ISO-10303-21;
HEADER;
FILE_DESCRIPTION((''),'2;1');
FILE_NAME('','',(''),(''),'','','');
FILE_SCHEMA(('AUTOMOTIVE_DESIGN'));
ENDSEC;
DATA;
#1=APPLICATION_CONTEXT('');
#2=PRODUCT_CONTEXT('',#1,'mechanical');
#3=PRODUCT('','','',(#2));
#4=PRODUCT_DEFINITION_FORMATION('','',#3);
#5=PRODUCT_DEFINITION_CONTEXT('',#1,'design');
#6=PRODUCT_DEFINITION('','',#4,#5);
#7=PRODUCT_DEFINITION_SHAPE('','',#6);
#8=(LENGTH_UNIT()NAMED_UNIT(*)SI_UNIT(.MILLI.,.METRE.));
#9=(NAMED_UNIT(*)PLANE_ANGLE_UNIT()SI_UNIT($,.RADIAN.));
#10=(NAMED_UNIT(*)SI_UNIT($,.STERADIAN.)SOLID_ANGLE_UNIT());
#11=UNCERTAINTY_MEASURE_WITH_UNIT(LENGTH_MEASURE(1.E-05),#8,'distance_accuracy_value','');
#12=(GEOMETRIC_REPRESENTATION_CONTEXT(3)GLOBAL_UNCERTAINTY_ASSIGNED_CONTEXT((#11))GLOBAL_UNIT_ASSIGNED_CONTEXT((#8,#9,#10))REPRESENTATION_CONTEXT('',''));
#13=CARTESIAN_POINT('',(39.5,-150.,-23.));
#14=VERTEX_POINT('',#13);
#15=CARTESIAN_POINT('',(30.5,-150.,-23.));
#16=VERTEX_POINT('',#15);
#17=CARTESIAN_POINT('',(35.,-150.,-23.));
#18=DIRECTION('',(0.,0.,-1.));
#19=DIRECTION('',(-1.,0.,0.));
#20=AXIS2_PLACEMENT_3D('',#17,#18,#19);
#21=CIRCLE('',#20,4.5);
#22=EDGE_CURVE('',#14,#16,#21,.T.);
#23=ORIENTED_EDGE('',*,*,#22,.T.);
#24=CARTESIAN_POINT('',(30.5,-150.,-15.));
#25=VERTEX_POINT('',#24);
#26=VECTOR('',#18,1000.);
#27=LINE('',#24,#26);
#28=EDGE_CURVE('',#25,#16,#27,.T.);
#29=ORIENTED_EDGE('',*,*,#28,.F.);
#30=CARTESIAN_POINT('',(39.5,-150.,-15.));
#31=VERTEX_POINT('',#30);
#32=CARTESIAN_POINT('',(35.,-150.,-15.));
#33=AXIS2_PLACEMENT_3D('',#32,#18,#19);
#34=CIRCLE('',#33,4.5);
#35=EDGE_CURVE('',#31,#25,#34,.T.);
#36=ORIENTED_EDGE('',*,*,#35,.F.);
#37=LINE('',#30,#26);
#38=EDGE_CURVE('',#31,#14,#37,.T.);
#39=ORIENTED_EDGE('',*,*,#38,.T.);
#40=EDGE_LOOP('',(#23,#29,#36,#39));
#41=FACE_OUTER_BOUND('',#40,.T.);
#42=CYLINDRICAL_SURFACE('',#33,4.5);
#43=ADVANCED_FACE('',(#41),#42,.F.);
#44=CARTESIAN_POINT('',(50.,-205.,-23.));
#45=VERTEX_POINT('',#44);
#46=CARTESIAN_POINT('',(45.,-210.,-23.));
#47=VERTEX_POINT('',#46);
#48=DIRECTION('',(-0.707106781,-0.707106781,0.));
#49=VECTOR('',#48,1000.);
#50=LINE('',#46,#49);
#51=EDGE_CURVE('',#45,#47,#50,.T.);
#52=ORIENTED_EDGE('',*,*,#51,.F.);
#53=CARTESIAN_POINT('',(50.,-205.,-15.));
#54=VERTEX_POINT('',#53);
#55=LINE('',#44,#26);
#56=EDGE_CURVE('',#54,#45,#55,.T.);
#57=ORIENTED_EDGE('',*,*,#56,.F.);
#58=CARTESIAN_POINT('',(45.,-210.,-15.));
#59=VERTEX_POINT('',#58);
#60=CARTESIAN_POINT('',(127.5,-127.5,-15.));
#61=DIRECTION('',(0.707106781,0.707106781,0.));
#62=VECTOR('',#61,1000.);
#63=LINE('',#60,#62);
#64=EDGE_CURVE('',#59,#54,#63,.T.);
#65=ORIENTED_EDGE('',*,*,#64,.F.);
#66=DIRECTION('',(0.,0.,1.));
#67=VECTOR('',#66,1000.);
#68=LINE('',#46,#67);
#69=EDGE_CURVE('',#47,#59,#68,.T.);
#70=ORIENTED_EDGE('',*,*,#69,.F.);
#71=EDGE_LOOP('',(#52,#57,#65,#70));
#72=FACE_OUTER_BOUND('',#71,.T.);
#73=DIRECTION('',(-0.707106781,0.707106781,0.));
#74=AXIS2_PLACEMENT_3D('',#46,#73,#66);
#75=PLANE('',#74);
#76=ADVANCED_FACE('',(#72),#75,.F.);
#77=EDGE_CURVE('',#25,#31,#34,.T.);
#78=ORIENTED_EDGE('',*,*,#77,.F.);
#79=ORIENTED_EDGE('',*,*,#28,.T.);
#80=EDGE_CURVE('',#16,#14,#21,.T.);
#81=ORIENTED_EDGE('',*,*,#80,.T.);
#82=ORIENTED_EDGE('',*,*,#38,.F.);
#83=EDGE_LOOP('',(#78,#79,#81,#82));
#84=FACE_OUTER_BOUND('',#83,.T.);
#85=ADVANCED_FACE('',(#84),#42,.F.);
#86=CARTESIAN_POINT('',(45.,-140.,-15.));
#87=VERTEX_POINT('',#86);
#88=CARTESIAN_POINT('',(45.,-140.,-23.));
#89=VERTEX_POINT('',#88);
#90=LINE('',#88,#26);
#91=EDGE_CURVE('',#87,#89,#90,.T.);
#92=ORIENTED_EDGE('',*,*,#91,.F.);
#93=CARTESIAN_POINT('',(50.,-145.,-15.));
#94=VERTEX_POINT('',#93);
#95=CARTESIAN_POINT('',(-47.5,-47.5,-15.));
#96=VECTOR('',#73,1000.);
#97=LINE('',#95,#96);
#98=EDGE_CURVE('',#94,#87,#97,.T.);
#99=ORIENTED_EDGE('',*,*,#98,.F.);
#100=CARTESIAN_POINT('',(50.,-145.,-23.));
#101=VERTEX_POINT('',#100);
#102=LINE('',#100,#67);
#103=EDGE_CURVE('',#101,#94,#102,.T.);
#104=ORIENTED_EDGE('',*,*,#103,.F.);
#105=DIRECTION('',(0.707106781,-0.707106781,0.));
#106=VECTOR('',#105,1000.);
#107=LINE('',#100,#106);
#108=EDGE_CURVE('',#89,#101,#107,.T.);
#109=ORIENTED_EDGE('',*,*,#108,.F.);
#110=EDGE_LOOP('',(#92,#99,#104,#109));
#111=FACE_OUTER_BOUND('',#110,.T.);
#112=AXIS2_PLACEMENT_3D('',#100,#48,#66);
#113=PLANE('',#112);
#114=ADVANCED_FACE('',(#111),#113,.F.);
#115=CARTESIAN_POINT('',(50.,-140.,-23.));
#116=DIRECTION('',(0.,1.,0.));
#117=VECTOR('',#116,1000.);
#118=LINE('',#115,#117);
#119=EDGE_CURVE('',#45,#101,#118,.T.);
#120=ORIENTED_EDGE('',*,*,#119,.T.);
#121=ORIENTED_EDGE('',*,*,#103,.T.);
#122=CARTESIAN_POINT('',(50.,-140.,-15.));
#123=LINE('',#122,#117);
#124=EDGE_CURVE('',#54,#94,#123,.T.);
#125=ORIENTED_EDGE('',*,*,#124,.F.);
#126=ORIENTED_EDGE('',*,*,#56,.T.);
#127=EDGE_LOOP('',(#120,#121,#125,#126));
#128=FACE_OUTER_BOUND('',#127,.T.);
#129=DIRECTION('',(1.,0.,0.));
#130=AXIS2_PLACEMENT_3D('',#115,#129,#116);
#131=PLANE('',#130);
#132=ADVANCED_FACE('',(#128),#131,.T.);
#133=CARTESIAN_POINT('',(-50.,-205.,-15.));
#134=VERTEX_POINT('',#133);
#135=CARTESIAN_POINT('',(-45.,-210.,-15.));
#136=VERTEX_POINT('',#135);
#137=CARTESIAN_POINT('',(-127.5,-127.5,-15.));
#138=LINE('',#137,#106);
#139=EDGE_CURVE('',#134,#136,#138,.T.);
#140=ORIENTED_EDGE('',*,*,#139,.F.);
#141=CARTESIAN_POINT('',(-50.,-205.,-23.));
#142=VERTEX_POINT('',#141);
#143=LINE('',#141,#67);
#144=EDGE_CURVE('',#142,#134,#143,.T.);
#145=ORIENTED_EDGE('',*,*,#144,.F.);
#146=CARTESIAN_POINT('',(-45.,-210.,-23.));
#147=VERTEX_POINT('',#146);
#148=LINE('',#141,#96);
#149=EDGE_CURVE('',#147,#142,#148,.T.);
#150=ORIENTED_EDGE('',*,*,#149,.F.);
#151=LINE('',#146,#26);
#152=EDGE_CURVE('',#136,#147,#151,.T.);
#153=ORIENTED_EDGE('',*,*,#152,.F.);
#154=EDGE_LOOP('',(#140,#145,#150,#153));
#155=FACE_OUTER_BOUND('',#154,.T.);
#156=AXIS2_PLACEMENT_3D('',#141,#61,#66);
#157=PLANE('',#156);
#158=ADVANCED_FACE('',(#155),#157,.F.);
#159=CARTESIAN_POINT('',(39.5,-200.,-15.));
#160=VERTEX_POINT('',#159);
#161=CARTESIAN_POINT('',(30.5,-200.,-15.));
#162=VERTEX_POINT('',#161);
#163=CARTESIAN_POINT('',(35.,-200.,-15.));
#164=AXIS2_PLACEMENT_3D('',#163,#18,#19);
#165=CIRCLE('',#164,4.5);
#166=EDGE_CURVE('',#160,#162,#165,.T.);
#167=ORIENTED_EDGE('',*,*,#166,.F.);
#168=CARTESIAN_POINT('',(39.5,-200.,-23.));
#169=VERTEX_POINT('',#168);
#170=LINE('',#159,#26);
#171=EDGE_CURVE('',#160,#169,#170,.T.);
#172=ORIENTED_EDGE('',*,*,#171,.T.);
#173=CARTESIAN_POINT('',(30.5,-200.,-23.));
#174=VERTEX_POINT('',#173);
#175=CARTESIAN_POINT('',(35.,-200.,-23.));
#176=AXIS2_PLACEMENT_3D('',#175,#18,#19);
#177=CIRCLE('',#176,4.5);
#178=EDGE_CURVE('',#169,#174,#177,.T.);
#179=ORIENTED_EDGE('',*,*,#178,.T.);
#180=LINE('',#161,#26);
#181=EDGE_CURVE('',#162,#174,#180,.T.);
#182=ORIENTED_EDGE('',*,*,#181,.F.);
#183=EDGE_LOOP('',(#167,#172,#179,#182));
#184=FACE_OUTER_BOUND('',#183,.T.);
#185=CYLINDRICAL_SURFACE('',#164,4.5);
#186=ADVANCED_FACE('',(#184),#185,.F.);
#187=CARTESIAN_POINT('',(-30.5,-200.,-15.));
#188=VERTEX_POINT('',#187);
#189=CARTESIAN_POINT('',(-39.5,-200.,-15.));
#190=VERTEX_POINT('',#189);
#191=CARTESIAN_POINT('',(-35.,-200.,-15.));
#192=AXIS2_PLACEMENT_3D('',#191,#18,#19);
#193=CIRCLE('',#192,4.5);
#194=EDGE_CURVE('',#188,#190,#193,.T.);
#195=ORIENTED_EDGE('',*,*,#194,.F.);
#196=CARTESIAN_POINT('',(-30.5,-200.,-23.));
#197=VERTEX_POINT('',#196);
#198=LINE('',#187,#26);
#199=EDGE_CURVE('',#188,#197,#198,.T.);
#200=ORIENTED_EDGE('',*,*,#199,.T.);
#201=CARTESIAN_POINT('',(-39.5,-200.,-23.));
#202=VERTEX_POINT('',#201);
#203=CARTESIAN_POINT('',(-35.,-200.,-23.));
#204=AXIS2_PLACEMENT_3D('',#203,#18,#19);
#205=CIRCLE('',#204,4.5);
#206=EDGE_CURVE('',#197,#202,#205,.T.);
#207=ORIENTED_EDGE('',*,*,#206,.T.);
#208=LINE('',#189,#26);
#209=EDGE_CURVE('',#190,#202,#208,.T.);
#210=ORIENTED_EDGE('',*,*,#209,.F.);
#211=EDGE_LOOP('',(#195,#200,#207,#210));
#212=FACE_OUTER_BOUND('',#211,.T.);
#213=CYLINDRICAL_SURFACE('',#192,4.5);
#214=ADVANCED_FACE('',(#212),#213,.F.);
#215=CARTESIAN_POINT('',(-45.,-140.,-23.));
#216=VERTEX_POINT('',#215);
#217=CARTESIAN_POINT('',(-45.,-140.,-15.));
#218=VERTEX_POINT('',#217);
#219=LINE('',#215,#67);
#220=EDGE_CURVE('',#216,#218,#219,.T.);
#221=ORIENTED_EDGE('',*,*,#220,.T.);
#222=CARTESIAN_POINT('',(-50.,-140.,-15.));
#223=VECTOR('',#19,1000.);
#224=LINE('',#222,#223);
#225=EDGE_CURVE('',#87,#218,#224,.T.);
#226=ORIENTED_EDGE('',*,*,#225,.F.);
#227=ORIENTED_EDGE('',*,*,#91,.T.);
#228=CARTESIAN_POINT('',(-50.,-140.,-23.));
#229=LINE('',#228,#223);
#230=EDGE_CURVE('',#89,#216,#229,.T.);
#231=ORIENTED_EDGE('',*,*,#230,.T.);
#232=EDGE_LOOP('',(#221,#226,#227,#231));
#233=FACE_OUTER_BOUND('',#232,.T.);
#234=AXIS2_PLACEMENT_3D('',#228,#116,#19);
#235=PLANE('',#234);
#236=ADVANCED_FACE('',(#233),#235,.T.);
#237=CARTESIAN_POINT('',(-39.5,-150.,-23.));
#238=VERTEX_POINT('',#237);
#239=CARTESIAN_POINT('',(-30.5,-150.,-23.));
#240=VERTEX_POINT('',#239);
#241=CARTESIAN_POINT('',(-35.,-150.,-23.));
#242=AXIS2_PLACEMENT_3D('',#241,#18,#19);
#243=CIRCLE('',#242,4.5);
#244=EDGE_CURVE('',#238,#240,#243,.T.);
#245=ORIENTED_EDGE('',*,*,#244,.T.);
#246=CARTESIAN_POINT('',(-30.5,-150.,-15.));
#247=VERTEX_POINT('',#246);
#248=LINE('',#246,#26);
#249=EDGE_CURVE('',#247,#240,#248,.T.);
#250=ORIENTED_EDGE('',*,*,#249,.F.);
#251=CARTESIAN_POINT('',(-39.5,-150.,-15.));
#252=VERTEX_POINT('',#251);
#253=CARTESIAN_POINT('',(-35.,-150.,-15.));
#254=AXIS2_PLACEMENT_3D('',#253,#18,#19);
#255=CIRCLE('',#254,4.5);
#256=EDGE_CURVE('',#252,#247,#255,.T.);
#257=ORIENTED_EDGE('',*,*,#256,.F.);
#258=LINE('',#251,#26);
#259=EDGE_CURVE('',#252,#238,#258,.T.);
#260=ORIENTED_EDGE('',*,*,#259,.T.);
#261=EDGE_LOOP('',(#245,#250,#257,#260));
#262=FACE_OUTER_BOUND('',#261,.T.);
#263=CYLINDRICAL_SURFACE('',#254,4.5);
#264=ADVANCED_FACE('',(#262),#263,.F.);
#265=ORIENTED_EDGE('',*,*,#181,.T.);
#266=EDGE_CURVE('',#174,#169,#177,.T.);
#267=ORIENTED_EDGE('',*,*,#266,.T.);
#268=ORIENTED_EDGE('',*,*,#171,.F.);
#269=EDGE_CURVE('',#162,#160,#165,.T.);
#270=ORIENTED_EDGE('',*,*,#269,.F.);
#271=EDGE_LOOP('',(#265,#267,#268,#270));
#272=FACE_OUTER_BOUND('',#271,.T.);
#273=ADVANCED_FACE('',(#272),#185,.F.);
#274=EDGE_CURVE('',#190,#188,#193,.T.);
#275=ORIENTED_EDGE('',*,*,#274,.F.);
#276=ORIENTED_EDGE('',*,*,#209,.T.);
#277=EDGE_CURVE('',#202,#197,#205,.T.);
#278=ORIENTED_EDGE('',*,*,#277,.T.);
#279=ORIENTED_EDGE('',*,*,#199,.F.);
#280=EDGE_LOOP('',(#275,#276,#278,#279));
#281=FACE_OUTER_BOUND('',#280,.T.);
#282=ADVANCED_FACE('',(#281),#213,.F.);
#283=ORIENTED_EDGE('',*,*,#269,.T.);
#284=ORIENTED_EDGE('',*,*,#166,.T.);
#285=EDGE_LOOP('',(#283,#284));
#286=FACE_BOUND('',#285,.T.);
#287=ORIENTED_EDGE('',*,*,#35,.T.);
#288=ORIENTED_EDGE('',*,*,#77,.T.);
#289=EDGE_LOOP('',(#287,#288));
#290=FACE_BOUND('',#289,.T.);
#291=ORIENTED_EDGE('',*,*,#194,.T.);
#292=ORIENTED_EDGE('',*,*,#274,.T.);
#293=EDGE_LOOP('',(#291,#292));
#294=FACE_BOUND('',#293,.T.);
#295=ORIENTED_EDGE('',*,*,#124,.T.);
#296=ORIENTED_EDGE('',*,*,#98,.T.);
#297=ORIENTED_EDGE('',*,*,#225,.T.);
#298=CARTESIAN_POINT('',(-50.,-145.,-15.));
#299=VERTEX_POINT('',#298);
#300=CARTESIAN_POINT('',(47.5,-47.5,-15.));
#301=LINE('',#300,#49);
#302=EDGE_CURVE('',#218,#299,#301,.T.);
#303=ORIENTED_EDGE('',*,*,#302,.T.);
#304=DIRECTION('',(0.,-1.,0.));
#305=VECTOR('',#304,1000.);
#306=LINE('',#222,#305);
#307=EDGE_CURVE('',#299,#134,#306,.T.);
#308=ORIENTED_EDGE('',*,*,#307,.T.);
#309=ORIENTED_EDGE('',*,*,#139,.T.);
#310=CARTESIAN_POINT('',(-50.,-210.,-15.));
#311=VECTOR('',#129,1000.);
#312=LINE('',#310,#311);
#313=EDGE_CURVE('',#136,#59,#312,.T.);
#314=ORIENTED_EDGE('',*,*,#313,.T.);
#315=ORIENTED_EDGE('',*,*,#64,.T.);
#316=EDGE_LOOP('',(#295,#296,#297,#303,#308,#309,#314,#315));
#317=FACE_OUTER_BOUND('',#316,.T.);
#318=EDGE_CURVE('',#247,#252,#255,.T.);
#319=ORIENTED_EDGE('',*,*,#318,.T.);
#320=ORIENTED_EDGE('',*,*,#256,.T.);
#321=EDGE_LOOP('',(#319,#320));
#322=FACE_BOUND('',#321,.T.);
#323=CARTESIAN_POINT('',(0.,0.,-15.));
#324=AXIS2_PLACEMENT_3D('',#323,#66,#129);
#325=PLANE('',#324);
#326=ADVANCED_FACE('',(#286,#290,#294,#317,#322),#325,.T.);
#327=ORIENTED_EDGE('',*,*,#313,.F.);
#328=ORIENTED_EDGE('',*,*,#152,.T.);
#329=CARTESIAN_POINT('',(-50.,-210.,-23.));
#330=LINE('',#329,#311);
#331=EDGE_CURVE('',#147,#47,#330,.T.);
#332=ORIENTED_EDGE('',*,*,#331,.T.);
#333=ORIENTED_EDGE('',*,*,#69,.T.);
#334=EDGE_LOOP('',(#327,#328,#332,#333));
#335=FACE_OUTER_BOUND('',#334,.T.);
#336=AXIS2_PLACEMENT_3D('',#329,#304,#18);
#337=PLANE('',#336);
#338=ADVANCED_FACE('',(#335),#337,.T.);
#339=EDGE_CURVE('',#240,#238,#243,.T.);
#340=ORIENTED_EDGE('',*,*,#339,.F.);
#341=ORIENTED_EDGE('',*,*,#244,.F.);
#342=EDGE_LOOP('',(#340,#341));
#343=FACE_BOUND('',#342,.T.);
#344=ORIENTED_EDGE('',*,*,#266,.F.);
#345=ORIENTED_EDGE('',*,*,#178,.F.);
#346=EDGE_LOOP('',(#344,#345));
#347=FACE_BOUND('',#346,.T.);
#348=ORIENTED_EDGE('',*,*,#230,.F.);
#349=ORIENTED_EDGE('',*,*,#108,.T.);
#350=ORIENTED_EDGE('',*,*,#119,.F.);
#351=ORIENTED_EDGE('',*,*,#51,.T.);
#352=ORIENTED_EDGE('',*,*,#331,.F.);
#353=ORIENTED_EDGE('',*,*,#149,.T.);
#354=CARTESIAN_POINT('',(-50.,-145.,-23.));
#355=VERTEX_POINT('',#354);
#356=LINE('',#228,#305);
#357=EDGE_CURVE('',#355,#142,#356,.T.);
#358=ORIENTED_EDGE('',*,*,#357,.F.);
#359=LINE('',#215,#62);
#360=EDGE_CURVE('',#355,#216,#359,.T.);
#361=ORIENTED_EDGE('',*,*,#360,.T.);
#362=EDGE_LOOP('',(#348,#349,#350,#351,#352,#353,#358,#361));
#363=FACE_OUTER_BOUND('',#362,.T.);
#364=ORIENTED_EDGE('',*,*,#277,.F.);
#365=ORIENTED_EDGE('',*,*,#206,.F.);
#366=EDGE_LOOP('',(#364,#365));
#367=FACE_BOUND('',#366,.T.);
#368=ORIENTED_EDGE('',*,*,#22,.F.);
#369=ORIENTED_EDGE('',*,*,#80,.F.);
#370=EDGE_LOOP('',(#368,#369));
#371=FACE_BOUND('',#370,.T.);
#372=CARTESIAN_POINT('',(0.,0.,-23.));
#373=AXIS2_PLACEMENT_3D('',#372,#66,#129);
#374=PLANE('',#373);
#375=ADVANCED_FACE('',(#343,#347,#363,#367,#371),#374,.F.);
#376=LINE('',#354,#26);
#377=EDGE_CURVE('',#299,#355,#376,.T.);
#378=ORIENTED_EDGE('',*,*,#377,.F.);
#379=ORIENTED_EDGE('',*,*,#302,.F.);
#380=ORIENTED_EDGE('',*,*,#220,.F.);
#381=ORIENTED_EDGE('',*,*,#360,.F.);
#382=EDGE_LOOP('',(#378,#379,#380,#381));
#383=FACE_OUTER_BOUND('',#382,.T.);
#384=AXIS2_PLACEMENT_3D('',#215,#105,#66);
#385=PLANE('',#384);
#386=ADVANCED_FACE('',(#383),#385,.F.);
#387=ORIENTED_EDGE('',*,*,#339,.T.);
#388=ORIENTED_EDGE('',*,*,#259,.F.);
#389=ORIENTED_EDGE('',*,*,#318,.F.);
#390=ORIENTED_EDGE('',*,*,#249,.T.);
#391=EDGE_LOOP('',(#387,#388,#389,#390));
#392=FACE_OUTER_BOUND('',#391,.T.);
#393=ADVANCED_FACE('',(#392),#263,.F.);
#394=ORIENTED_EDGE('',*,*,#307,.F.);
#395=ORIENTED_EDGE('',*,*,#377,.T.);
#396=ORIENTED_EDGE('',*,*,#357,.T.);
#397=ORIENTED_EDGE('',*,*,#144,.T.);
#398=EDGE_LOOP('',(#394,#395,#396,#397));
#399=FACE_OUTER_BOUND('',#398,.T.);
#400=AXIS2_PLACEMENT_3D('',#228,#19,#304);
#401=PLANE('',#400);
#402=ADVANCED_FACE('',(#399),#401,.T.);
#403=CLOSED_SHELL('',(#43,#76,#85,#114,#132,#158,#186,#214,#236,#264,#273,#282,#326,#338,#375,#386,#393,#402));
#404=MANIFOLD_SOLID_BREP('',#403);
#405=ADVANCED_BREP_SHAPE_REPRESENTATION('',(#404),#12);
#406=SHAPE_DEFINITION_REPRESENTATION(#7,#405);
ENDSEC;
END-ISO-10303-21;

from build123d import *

# Parameters (mm, degrees)
SKETCH1_W           = 100
SKETCH1_H           = 70
BOSS_EXTRUDE1_DEPTH = 8
SKETCH2_R           = 4.5
CUT_EXTRUDE1_DEPTH  = 8
CHAMFER1_SIZE       = 5


with BuildPart() as part:
    # Sketch1 → Boss-Extrude1 (new body)
    with BuildSketch(Plane.XY.offset(-15)):
        with Locations((0, -175)):
            Rectangle(SKETCH1_W, SKETCH1_H)
    extrude(amount=-BOSS_EXTRUDE1_DEPTH)

    # Sketch2 → Cut-Extrude1 (cut)
    with BuildSketch(Plane(origin=(0, 0, -23), x_dir=(-1, 0, 0), z_dir=(0, 0, -1))):
        with Locations((-35, -150)):
            Circle(SKETCH2_R)
        with Locations((35, -150)):
            Circle(SKETCH2_R)
        with Locations((35, -200)):
            Circle(SKETCH2_R)
        with Locations((-35, -200)):
            Circle(SKETCH2_R)
    extrude(amount=-CUT_EXTRUDE1_DEPTH, mode=Mode.SUBTRACT)

    # Chamfer1
    chamfer1_edges = [part.edges().sort_by_distance(p)[0] for p in [
        (50, -210, -19),
        (-50, -210, -19),
        (-50, -140, -19),
        (50, -140, -19),
    ]]
    chamfer(chamfer1_edges, length=CHAMFER1_SIZE)


solid = part.part
